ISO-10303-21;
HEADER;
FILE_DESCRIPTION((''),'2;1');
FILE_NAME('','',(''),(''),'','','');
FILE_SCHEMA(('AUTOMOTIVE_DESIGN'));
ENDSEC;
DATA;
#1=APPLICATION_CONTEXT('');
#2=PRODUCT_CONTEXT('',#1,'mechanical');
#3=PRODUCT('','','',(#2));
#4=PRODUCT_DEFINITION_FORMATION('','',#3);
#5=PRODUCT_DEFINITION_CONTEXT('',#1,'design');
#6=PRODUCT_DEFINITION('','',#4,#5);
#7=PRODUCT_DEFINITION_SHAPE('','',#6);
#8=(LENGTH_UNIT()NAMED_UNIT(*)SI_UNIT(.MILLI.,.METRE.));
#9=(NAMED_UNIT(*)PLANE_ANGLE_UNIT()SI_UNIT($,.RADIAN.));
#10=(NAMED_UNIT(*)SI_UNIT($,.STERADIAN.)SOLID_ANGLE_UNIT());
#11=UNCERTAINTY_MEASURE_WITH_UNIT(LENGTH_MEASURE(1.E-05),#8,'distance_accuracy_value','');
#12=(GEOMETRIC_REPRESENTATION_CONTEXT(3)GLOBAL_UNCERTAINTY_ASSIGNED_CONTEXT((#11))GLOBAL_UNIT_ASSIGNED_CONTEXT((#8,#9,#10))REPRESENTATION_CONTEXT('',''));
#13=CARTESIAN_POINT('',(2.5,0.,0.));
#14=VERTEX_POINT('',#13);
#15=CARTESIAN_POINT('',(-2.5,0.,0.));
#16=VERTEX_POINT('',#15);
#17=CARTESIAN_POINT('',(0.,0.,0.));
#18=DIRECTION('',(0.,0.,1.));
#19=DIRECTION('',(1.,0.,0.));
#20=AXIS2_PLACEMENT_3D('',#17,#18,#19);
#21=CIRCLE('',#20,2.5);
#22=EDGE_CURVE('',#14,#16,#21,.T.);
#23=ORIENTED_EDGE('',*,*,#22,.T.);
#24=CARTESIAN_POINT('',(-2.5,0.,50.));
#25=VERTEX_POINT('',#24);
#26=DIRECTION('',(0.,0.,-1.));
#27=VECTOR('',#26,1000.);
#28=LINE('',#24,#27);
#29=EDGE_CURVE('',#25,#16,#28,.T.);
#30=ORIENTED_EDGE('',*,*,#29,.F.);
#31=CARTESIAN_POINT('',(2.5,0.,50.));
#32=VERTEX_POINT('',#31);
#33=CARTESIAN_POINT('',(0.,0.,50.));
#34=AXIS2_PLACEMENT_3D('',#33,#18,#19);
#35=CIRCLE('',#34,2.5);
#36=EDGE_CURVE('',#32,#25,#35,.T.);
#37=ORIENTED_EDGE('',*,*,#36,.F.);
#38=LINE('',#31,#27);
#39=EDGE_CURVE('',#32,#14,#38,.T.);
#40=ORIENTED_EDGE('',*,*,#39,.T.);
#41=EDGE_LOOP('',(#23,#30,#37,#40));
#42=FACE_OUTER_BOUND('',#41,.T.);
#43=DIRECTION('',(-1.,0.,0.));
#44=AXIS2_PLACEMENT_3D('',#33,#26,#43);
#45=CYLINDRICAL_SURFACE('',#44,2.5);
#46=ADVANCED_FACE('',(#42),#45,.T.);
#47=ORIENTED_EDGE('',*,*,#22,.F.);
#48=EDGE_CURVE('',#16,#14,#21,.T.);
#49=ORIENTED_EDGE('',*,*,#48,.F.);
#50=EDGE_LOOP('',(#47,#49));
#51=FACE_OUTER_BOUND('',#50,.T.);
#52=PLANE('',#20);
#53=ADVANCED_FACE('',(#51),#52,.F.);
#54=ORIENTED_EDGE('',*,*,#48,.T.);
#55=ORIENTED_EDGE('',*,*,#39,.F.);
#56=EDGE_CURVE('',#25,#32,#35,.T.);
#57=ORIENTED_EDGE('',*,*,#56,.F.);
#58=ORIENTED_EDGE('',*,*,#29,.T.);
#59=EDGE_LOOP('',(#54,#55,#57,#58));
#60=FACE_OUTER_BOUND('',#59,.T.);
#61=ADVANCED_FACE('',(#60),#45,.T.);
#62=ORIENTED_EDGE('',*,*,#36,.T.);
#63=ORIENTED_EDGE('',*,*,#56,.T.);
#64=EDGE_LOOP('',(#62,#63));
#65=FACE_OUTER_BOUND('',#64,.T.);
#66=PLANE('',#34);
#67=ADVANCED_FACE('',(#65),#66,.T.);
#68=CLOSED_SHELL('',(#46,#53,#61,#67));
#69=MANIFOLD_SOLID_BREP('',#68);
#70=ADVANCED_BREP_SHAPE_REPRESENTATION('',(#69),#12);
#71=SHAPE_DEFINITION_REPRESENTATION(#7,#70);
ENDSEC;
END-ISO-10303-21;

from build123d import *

# Parameters (mm, degrees)
SKETCH1_R           = 2.5
BOSS_EXTRUDE1_DEPTH = 50


with BuildPart() as part:
    # Sketch1 → Boss-Extrude1 (new body)
    with BuildSketch(Plane.XY):
        Circle(SKETCH1_R)
    extrude(amount=BOSS_EXTRUDE1_DEPTH)


solid = part.part
